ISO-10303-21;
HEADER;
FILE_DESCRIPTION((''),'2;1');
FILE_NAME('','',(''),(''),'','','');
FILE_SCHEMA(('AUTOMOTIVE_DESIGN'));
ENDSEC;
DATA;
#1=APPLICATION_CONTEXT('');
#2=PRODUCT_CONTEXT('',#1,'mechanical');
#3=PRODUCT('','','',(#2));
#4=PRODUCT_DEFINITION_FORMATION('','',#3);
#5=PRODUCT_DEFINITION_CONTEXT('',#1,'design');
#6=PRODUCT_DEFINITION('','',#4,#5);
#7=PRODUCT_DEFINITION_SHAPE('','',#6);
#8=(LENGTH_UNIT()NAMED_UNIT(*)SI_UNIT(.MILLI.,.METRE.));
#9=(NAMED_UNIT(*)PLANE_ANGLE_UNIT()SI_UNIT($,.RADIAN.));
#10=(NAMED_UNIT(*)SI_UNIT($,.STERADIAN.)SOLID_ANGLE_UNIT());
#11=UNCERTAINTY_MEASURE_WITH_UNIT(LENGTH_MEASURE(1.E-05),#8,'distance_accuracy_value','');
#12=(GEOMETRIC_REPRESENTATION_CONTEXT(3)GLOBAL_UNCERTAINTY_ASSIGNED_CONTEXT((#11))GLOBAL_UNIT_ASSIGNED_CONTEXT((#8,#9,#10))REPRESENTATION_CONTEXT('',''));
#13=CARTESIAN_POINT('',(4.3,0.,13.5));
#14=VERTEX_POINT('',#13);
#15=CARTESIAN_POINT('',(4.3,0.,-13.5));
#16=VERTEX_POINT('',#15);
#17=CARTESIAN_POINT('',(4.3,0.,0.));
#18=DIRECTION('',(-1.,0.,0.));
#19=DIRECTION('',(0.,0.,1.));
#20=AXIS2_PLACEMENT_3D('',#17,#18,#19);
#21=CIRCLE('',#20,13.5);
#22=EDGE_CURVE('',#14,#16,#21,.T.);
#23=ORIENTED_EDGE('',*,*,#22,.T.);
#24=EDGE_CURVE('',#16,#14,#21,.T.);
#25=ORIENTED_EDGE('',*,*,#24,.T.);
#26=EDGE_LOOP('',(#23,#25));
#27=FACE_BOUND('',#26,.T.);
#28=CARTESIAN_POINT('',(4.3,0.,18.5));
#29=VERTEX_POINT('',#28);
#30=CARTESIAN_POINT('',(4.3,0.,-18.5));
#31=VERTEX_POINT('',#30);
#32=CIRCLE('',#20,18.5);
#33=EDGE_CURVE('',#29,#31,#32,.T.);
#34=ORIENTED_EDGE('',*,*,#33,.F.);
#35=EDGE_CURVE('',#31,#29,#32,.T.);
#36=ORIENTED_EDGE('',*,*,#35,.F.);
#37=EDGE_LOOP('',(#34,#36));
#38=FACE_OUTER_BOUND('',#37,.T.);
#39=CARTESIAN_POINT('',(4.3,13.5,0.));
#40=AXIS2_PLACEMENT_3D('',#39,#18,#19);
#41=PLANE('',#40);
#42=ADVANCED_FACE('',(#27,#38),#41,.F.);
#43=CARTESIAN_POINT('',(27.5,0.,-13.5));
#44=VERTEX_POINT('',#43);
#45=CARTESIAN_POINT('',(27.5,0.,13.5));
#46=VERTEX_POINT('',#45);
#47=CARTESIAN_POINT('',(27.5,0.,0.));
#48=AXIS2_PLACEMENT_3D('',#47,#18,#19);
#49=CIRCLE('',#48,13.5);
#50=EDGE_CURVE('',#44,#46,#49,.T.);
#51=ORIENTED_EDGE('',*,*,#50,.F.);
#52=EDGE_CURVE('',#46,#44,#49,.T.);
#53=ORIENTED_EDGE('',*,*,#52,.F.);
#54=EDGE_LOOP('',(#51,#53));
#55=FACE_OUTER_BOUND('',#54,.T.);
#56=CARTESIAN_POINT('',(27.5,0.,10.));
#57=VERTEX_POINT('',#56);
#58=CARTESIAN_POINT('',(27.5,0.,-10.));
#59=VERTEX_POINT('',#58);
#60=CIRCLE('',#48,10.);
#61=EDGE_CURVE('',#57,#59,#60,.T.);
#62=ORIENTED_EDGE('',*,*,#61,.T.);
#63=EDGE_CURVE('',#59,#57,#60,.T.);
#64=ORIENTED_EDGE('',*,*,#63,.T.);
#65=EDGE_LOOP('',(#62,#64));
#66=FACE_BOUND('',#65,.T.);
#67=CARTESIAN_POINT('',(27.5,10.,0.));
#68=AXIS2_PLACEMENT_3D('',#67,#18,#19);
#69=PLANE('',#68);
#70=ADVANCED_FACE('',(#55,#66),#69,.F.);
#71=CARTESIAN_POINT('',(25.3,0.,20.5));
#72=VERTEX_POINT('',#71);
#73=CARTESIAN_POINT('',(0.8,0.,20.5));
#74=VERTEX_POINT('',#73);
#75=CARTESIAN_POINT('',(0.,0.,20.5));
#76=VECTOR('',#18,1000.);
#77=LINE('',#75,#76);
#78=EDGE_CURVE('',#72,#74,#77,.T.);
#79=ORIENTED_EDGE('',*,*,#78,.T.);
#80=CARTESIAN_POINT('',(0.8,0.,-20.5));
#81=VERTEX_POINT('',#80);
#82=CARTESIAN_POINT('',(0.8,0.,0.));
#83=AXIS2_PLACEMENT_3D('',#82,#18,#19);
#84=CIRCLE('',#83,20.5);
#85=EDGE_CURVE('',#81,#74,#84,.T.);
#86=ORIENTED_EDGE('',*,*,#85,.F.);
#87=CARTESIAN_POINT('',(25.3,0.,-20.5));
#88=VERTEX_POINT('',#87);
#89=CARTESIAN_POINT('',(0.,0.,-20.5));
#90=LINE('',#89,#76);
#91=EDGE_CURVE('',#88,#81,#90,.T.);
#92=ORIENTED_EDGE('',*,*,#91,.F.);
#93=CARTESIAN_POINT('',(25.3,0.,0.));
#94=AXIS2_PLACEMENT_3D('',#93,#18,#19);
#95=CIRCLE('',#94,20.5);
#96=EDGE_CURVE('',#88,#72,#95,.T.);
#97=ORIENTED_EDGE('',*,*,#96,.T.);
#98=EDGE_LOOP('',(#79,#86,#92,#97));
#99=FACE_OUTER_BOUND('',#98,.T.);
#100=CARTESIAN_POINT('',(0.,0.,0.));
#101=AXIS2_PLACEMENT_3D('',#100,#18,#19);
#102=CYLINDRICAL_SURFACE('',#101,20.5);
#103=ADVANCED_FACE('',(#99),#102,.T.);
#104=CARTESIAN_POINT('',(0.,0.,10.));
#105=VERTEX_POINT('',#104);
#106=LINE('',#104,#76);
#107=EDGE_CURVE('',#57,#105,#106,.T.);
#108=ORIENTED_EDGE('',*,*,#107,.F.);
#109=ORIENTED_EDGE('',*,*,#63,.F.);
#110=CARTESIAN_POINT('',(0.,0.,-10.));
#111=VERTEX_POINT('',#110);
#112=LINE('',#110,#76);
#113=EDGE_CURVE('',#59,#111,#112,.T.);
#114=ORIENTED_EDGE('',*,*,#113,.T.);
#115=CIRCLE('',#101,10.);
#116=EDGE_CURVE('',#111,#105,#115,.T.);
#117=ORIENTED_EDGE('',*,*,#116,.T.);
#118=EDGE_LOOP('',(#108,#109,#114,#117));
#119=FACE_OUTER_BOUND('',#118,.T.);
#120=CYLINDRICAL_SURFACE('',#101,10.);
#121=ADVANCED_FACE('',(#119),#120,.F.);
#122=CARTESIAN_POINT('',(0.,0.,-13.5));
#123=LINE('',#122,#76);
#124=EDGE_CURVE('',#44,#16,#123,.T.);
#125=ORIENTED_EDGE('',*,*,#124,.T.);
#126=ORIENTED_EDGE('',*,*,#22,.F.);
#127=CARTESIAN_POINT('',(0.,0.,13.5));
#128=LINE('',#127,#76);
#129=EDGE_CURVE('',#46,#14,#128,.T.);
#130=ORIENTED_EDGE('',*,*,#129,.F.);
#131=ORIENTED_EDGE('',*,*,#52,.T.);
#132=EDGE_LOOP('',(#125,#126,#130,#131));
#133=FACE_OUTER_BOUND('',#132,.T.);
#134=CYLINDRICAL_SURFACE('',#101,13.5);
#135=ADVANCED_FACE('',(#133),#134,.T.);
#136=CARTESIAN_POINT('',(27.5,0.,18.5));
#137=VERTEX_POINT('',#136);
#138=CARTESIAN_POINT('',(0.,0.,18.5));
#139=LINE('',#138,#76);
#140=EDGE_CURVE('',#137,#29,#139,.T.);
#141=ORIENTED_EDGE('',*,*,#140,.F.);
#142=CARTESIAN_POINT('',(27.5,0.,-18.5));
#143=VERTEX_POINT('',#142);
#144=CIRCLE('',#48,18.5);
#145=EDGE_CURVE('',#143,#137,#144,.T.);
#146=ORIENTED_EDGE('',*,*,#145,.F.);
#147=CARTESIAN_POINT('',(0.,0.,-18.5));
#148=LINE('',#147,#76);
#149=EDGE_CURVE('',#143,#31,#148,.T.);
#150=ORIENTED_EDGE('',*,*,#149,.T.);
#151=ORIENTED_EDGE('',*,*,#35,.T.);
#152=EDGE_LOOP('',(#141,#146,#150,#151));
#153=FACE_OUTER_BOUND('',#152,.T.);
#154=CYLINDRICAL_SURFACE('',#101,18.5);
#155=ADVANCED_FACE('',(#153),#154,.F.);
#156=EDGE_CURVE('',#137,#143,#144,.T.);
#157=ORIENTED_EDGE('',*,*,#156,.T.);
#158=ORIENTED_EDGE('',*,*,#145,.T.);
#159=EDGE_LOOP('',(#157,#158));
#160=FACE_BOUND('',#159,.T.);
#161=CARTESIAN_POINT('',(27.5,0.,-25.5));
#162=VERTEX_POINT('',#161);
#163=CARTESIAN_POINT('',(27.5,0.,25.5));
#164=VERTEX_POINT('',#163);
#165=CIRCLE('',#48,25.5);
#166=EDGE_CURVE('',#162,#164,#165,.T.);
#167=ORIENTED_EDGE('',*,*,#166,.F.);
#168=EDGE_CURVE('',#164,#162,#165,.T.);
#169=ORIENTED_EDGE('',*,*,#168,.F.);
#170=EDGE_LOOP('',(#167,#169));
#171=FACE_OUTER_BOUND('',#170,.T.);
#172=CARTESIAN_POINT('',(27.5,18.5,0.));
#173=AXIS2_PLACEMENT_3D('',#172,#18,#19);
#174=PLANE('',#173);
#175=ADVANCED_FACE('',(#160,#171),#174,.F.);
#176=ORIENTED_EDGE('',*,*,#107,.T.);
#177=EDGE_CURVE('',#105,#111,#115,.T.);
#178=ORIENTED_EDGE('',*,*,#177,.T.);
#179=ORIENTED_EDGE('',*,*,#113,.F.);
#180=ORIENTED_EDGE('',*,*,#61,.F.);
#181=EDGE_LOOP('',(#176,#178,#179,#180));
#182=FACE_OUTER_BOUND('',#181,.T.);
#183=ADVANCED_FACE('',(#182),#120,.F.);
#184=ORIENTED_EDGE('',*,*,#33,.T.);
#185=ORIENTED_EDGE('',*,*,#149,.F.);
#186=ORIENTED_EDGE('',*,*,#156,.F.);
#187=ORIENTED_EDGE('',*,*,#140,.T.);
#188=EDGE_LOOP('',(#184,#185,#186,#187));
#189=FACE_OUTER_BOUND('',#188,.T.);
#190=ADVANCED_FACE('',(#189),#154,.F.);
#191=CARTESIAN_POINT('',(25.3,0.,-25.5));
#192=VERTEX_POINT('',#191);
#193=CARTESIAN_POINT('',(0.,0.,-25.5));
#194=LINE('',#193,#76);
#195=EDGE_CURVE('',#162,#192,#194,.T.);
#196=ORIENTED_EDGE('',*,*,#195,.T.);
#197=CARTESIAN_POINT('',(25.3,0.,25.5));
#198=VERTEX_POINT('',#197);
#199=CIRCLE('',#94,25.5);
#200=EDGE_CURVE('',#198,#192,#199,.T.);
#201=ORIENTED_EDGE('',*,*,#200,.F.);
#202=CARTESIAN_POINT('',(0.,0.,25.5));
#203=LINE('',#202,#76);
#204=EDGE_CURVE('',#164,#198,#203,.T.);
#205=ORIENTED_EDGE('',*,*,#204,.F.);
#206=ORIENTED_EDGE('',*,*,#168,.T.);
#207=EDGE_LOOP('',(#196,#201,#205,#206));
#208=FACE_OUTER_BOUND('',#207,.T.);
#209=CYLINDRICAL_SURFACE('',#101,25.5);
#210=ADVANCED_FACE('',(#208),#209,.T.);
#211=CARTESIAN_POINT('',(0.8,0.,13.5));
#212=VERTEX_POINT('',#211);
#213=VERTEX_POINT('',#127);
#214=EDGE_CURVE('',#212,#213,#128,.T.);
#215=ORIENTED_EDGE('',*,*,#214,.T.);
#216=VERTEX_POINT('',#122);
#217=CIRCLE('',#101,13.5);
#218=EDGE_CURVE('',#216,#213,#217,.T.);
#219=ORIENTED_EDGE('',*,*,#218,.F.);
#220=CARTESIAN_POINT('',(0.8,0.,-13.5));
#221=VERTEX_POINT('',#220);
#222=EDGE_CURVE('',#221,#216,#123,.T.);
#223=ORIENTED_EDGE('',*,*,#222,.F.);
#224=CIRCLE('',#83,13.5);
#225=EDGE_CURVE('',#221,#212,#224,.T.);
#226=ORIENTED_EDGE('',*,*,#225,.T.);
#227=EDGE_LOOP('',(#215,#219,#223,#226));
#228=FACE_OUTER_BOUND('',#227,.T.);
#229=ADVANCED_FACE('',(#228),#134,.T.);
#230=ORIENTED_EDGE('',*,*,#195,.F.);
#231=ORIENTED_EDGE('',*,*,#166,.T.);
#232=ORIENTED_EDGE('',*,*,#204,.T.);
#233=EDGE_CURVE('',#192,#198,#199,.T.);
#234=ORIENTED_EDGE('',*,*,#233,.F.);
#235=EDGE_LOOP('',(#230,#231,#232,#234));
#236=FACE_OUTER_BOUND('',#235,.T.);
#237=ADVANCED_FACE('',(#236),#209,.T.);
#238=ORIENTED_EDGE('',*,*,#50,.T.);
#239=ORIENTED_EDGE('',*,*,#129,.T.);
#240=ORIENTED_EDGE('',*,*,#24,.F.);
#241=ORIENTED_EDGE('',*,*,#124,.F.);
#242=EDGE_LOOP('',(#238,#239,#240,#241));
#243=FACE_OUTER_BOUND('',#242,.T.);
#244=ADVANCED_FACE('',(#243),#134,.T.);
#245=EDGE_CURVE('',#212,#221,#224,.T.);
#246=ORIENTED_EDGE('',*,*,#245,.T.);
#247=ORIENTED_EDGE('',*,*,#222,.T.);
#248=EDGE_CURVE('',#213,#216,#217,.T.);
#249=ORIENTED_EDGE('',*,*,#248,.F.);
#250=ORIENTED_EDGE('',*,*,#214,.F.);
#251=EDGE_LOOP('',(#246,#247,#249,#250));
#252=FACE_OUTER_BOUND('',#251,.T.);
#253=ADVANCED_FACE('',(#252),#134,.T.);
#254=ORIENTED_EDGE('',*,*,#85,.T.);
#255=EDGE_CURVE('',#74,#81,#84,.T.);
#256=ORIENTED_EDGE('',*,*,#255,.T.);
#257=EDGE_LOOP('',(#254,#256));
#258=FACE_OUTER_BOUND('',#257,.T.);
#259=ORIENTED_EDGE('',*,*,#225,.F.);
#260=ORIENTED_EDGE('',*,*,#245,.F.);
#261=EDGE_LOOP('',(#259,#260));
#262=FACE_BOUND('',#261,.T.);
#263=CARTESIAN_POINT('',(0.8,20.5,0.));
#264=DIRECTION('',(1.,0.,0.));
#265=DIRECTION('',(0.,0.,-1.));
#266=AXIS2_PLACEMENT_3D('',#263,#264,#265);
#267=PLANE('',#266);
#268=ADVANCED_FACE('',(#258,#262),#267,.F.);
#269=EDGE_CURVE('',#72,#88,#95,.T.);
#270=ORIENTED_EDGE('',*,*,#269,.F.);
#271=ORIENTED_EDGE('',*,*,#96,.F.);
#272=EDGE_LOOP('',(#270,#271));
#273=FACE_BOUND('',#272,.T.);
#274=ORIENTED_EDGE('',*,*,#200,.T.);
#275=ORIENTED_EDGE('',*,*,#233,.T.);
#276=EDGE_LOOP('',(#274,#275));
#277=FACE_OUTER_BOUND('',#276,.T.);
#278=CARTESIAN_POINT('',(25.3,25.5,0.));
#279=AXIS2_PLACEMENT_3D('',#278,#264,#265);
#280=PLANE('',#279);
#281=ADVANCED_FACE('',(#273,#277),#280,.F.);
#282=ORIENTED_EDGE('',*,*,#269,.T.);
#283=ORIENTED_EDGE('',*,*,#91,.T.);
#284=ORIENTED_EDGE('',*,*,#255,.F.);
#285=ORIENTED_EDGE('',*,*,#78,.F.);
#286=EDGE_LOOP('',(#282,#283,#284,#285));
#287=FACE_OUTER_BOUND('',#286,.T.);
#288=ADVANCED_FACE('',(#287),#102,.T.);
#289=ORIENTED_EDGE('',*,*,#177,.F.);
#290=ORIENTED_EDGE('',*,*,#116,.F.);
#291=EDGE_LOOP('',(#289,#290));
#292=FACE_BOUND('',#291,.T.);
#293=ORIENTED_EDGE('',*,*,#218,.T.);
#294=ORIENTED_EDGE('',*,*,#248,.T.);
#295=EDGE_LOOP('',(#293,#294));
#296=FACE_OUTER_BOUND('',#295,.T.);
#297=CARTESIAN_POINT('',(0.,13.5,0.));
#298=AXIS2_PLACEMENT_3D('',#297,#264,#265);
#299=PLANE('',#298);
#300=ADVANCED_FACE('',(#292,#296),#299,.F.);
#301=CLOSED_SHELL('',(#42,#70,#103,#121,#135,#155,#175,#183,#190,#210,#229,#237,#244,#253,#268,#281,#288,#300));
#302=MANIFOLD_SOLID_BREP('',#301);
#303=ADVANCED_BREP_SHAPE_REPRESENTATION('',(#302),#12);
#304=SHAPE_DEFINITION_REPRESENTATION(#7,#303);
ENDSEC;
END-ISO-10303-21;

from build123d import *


with BuildPart() as part:
    # 草图1 → 旋转1 (revolve)
    with BuildSketch(Plane.XY, mode=Mode.PRIVATE) as revolve_1_sk:
        Polygon((25.3, 25.5), (25.3, 20.5), (0.8, 20.5), (0.8, 13.5), (0, 13.5), (0, 10), (27.5, 10), (27.5, 13.5), (4.3, 13.5), (4.3, 18.5), (27.5, 18.5), (27.5, 25.5), align=None)
    revolve(revolve_1_sk.sketch.rotate(Axis((0, 0, 0), (1, 0, 0)), 90), axis=Axis((0, 0, 0), (1, 0, 0)))


solid = part.part
